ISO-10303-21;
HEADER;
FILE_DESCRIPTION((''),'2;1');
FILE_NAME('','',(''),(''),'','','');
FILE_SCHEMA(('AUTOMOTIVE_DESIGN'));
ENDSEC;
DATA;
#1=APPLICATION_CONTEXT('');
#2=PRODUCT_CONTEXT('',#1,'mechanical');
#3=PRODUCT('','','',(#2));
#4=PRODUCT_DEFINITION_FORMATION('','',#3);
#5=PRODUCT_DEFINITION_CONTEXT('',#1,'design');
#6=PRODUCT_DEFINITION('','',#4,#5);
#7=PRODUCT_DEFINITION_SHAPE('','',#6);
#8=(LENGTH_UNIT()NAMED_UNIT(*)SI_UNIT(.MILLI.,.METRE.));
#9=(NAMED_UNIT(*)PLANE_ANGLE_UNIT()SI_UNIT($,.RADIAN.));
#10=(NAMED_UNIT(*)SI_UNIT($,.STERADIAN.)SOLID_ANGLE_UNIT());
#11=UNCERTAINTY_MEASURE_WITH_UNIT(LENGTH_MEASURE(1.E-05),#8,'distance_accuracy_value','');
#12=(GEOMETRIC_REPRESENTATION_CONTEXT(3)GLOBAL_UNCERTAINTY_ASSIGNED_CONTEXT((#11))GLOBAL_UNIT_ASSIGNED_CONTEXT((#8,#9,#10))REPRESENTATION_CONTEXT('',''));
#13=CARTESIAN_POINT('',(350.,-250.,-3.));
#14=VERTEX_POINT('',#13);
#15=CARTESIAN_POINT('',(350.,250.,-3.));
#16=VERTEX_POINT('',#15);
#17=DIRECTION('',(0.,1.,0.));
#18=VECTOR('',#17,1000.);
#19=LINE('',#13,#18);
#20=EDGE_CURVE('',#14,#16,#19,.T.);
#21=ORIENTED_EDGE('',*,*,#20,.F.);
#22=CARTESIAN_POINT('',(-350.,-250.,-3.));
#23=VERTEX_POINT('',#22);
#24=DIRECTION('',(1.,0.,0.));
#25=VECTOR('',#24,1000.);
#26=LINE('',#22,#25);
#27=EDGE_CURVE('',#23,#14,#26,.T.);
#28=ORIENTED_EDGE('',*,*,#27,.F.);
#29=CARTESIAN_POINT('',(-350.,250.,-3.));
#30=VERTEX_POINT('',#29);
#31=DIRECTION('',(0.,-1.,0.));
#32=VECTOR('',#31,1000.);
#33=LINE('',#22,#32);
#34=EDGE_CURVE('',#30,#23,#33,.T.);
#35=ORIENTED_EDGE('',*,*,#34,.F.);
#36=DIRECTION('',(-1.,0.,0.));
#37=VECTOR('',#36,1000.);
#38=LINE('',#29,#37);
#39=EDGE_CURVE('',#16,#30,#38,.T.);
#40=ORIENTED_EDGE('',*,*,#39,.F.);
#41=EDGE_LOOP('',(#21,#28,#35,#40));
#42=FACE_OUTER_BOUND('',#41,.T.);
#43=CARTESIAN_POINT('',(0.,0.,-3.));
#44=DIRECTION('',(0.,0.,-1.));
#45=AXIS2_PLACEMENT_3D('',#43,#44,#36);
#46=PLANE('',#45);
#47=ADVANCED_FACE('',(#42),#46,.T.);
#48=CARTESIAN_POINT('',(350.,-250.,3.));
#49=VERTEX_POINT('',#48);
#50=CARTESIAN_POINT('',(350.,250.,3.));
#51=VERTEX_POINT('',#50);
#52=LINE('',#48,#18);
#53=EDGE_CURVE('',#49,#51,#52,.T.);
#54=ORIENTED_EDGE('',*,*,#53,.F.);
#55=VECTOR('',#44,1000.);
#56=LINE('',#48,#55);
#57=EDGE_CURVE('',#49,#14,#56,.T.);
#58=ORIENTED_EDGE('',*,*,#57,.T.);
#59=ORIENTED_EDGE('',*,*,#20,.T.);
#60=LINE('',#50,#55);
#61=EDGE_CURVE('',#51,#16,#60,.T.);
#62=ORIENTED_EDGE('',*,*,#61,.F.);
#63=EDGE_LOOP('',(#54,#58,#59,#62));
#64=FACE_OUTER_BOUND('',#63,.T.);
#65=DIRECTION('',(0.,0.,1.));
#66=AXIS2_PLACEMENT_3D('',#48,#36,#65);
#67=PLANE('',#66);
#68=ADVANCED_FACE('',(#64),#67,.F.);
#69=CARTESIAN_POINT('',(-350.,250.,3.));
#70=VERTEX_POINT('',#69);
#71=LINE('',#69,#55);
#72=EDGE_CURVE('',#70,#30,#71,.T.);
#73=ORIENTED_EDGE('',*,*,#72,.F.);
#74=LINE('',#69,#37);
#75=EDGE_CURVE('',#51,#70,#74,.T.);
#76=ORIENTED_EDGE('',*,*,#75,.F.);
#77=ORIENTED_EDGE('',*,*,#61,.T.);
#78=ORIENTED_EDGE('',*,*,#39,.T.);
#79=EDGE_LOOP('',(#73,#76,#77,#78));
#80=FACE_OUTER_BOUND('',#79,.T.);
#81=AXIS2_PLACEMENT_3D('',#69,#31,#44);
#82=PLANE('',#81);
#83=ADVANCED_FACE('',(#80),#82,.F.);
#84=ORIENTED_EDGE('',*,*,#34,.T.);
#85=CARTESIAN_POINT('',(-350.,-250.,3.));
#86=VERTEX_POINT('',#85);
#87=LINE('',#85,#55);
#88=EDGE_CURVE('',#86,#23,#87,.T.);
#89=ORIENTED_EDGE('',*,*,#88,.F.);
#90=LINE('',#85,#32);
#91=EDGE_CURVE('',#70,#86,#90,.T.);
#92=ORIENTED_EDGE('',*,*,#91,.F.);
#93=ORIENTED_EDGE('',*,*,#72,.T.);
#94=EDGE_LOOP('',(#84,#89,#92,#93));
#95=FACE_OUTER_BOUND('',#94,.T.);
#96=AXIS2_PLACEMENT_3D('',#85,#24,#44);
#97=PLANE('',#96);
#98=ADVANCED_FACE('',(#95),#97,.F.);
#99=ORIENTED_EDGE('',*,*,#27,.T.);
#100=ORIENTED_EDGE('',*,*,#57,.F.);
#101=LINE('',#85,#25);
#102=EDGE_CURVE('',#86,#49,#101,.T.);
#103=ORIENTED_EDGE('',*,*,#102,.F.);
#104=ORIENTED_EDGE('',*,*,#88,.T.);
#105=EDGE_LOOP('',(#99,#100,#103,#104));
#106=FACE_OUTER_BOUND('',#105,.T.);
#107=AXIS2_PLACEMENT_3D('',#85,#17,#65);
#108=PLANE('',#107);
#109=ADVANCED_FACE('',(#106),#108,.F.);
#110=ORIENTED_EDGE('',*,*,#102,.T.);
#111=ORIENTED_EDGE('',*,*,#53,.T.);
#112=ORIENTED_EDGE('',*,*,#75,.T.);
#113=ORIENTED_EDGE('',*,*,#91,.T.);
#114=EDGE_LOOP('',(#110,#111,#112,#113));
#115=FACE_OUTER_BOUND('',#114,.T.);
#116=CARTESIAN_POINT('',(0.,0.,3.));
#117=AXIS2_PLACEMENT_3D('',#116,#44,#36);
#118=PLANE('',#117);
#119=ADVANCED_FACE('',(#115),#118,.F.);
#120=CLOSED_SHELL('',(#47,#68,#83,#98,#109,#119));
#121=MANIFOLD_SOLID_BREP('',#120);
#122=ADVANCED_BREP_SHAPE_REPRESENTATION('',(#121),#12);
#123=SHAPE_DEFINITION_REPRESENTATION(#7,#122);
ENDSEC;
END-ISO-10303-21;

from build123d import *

# Parameters (mm, degrees)
SKETCH1_W           = 700
SKETCH1_H           = 500
BOSS_EXTRUDE1_DEPTH = 3


with BuildPart() as part:
    # Sketch1 → Boss-Extrude1 (new, symmetric)
    with BuildSketch(Plane.XY):
        Rectangle(SKETCH1_W, SKETCH1_H)
    extrude(amount=BOSS_EXTRUDE1_DEPTH, both=True)


solid = part.part
